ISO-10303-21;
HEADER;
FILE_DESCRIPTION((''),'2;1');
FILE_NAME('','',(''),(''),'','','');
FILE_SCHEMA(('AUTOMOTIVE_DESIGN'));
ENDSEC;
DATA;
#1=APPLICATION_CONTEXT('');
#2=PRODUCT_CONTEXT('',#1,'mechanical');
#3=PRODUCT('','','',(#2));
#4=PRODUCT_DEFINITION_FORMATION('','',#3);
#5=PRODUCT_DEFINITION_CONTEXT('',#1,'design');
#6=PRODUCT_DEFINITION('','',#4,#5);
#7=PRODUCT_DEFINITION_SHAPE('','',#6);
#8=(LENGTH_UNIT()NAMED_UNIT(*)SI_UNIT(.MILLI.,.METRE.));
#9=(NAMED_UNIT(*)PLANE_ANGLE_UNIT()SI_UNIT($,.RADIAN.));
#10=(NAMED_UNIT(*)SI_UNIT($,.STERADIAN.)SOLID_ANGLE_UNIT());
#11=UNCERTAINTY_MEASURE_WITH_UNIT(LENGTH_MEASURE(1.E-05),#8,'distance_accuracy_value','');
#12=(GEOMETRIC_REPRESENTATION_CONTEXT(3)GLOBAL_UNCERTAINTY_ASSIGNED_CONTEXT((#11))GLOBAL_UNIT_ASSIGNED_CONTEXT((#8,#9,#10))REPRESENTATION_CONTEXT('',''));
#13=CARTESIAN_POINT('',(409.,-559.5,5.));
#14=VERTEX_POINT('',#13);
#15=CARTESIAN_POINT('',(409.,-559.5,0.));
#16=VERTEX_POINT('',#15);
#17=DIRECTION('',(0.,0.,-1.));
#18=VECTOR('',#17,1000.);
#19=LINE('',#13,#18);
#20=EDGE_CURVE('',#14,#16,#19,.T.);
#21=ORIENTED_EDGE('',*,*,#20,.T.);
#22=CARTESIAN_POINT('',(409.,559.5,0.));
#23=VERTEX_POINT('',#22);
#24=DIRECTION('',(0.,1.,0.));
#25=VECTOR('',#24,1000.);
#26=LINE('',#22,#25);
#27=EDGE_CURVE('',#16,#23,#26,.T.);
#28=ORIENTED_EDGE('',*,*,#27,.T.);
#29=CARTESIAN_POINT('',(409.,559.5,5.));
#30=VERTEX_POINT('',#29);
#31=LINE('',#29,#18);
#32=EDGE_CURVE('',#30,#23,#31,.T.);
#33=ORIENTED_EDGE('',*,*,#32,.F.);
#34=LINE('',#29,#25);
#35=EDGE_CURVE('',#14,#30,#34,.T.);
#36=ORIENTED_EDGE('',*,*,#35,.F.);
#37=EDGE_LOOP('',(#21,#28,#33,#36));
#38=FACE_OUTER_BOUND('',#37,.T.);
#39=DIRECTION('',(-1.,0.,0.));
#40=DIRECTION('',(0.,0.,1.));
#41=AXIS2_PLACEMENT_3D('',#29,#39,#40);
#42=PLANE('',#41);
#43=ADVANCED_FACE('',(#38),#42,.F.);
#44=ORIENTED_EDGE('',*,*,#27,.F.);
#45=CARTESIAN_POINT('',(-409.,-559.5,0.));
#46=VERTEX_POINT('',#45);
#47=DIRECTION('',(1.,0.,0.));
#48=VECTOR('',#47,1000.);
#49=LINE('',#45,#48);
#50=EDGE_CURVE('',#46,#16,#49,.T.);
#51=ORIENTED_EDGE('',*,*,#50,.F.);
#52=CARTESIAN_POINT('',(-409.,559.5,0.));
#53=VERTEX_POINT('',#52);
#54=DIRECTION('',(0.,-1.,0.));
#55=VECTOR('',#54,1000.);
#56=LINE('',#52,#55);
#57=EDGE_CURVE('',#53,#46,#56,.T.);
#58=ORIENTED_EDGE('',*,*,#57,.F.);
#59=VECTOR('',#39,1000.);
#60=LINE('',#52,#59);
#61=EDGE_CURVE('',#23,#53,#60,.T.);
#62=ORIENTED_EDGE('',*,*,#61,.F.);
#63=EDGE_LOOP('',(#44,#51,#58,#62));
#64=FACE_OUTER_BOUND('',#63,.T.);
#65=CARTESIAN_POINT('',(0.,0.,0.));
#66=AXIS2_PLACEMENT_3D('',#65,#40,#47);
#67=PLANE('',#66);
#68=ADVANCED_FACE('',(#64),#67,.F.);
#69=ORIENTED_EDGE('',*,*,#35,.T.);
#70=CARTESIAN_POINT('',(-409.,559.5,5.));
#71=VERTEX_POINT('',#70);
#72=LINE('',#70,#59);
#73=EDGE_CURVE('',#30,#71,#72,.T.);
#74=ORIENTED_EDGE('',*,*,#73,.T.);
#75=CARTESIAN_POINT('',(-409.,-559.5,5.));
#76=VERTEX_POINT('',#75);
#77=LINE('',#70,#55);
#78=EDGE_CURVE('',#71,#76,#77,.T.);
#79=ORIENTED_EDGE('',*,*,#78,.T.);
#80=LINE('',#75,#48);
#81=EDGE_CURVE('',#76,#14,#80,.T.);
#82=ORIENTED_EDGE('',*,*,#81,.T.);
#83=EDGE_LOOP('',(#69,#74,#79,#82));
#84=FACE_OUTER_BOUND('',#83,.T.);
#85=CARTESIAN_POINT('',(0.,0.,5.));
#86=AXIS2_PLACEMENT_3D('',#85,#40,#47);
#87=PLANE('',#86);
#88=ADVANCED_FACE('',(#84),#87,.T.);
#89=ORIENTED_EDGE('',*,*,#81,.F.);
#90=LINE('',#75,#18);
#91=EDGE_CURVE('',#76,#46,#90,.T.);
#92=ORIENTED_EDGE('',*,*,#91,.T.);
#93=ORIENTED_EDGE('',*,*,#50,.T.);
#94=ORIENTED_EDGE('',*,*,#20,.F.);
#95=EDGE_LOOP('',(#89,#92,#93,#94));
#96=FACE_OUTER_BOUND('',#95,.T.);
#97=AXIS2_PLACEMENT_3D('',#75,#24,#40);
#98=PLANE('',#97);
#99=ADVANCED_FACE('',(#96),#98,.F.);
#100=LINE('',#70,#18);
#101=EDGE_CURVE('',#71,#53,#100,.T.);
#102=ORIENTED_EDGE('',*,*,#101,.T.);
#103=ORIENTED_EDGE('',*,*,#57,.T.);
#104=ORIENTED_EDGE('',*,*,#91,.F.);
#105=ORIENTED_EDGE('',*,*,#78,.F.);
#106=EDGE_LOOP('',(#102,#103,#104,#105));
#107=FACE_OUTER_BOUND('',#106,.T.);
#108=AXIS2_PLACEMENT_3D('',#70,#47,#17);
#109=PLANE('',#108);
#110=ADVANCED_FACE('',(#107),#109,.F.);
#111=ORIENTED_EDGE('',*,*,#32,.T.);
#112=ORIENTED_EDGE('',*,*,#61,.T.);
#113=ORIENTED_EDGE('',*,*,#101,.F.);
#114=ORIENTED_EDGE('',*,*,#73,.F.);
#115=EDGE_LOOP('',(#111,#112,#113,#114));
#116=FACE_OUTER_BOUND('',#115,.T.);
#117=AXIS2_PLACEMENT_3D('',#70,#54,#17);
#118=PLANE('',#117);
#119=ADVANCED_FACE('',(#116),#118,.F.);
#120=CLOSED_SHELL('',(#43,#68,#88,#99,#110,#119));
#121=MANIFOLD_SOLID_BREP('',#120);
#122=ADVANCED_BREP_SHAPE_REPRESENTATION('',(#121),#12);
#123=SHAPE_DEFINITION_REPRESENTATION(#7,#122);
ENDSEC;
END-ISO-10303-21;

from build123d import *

# Parameters (mm, degrees)
SKETCH_1_W      = 818
SKETCH_1_H      = 1119
EXTRUDE_1_DEPTH = 5


with BuildPart() as part:
    # 草图1 → 凸台-拉伸1 (new body)
    with BuildSketch(Plane.XY):
        Rectangle(SKETCH_1_W, SKETCH_1_H)
    extrude(amount=EXTRUDE_1_DEPTH)


solid = part.part
